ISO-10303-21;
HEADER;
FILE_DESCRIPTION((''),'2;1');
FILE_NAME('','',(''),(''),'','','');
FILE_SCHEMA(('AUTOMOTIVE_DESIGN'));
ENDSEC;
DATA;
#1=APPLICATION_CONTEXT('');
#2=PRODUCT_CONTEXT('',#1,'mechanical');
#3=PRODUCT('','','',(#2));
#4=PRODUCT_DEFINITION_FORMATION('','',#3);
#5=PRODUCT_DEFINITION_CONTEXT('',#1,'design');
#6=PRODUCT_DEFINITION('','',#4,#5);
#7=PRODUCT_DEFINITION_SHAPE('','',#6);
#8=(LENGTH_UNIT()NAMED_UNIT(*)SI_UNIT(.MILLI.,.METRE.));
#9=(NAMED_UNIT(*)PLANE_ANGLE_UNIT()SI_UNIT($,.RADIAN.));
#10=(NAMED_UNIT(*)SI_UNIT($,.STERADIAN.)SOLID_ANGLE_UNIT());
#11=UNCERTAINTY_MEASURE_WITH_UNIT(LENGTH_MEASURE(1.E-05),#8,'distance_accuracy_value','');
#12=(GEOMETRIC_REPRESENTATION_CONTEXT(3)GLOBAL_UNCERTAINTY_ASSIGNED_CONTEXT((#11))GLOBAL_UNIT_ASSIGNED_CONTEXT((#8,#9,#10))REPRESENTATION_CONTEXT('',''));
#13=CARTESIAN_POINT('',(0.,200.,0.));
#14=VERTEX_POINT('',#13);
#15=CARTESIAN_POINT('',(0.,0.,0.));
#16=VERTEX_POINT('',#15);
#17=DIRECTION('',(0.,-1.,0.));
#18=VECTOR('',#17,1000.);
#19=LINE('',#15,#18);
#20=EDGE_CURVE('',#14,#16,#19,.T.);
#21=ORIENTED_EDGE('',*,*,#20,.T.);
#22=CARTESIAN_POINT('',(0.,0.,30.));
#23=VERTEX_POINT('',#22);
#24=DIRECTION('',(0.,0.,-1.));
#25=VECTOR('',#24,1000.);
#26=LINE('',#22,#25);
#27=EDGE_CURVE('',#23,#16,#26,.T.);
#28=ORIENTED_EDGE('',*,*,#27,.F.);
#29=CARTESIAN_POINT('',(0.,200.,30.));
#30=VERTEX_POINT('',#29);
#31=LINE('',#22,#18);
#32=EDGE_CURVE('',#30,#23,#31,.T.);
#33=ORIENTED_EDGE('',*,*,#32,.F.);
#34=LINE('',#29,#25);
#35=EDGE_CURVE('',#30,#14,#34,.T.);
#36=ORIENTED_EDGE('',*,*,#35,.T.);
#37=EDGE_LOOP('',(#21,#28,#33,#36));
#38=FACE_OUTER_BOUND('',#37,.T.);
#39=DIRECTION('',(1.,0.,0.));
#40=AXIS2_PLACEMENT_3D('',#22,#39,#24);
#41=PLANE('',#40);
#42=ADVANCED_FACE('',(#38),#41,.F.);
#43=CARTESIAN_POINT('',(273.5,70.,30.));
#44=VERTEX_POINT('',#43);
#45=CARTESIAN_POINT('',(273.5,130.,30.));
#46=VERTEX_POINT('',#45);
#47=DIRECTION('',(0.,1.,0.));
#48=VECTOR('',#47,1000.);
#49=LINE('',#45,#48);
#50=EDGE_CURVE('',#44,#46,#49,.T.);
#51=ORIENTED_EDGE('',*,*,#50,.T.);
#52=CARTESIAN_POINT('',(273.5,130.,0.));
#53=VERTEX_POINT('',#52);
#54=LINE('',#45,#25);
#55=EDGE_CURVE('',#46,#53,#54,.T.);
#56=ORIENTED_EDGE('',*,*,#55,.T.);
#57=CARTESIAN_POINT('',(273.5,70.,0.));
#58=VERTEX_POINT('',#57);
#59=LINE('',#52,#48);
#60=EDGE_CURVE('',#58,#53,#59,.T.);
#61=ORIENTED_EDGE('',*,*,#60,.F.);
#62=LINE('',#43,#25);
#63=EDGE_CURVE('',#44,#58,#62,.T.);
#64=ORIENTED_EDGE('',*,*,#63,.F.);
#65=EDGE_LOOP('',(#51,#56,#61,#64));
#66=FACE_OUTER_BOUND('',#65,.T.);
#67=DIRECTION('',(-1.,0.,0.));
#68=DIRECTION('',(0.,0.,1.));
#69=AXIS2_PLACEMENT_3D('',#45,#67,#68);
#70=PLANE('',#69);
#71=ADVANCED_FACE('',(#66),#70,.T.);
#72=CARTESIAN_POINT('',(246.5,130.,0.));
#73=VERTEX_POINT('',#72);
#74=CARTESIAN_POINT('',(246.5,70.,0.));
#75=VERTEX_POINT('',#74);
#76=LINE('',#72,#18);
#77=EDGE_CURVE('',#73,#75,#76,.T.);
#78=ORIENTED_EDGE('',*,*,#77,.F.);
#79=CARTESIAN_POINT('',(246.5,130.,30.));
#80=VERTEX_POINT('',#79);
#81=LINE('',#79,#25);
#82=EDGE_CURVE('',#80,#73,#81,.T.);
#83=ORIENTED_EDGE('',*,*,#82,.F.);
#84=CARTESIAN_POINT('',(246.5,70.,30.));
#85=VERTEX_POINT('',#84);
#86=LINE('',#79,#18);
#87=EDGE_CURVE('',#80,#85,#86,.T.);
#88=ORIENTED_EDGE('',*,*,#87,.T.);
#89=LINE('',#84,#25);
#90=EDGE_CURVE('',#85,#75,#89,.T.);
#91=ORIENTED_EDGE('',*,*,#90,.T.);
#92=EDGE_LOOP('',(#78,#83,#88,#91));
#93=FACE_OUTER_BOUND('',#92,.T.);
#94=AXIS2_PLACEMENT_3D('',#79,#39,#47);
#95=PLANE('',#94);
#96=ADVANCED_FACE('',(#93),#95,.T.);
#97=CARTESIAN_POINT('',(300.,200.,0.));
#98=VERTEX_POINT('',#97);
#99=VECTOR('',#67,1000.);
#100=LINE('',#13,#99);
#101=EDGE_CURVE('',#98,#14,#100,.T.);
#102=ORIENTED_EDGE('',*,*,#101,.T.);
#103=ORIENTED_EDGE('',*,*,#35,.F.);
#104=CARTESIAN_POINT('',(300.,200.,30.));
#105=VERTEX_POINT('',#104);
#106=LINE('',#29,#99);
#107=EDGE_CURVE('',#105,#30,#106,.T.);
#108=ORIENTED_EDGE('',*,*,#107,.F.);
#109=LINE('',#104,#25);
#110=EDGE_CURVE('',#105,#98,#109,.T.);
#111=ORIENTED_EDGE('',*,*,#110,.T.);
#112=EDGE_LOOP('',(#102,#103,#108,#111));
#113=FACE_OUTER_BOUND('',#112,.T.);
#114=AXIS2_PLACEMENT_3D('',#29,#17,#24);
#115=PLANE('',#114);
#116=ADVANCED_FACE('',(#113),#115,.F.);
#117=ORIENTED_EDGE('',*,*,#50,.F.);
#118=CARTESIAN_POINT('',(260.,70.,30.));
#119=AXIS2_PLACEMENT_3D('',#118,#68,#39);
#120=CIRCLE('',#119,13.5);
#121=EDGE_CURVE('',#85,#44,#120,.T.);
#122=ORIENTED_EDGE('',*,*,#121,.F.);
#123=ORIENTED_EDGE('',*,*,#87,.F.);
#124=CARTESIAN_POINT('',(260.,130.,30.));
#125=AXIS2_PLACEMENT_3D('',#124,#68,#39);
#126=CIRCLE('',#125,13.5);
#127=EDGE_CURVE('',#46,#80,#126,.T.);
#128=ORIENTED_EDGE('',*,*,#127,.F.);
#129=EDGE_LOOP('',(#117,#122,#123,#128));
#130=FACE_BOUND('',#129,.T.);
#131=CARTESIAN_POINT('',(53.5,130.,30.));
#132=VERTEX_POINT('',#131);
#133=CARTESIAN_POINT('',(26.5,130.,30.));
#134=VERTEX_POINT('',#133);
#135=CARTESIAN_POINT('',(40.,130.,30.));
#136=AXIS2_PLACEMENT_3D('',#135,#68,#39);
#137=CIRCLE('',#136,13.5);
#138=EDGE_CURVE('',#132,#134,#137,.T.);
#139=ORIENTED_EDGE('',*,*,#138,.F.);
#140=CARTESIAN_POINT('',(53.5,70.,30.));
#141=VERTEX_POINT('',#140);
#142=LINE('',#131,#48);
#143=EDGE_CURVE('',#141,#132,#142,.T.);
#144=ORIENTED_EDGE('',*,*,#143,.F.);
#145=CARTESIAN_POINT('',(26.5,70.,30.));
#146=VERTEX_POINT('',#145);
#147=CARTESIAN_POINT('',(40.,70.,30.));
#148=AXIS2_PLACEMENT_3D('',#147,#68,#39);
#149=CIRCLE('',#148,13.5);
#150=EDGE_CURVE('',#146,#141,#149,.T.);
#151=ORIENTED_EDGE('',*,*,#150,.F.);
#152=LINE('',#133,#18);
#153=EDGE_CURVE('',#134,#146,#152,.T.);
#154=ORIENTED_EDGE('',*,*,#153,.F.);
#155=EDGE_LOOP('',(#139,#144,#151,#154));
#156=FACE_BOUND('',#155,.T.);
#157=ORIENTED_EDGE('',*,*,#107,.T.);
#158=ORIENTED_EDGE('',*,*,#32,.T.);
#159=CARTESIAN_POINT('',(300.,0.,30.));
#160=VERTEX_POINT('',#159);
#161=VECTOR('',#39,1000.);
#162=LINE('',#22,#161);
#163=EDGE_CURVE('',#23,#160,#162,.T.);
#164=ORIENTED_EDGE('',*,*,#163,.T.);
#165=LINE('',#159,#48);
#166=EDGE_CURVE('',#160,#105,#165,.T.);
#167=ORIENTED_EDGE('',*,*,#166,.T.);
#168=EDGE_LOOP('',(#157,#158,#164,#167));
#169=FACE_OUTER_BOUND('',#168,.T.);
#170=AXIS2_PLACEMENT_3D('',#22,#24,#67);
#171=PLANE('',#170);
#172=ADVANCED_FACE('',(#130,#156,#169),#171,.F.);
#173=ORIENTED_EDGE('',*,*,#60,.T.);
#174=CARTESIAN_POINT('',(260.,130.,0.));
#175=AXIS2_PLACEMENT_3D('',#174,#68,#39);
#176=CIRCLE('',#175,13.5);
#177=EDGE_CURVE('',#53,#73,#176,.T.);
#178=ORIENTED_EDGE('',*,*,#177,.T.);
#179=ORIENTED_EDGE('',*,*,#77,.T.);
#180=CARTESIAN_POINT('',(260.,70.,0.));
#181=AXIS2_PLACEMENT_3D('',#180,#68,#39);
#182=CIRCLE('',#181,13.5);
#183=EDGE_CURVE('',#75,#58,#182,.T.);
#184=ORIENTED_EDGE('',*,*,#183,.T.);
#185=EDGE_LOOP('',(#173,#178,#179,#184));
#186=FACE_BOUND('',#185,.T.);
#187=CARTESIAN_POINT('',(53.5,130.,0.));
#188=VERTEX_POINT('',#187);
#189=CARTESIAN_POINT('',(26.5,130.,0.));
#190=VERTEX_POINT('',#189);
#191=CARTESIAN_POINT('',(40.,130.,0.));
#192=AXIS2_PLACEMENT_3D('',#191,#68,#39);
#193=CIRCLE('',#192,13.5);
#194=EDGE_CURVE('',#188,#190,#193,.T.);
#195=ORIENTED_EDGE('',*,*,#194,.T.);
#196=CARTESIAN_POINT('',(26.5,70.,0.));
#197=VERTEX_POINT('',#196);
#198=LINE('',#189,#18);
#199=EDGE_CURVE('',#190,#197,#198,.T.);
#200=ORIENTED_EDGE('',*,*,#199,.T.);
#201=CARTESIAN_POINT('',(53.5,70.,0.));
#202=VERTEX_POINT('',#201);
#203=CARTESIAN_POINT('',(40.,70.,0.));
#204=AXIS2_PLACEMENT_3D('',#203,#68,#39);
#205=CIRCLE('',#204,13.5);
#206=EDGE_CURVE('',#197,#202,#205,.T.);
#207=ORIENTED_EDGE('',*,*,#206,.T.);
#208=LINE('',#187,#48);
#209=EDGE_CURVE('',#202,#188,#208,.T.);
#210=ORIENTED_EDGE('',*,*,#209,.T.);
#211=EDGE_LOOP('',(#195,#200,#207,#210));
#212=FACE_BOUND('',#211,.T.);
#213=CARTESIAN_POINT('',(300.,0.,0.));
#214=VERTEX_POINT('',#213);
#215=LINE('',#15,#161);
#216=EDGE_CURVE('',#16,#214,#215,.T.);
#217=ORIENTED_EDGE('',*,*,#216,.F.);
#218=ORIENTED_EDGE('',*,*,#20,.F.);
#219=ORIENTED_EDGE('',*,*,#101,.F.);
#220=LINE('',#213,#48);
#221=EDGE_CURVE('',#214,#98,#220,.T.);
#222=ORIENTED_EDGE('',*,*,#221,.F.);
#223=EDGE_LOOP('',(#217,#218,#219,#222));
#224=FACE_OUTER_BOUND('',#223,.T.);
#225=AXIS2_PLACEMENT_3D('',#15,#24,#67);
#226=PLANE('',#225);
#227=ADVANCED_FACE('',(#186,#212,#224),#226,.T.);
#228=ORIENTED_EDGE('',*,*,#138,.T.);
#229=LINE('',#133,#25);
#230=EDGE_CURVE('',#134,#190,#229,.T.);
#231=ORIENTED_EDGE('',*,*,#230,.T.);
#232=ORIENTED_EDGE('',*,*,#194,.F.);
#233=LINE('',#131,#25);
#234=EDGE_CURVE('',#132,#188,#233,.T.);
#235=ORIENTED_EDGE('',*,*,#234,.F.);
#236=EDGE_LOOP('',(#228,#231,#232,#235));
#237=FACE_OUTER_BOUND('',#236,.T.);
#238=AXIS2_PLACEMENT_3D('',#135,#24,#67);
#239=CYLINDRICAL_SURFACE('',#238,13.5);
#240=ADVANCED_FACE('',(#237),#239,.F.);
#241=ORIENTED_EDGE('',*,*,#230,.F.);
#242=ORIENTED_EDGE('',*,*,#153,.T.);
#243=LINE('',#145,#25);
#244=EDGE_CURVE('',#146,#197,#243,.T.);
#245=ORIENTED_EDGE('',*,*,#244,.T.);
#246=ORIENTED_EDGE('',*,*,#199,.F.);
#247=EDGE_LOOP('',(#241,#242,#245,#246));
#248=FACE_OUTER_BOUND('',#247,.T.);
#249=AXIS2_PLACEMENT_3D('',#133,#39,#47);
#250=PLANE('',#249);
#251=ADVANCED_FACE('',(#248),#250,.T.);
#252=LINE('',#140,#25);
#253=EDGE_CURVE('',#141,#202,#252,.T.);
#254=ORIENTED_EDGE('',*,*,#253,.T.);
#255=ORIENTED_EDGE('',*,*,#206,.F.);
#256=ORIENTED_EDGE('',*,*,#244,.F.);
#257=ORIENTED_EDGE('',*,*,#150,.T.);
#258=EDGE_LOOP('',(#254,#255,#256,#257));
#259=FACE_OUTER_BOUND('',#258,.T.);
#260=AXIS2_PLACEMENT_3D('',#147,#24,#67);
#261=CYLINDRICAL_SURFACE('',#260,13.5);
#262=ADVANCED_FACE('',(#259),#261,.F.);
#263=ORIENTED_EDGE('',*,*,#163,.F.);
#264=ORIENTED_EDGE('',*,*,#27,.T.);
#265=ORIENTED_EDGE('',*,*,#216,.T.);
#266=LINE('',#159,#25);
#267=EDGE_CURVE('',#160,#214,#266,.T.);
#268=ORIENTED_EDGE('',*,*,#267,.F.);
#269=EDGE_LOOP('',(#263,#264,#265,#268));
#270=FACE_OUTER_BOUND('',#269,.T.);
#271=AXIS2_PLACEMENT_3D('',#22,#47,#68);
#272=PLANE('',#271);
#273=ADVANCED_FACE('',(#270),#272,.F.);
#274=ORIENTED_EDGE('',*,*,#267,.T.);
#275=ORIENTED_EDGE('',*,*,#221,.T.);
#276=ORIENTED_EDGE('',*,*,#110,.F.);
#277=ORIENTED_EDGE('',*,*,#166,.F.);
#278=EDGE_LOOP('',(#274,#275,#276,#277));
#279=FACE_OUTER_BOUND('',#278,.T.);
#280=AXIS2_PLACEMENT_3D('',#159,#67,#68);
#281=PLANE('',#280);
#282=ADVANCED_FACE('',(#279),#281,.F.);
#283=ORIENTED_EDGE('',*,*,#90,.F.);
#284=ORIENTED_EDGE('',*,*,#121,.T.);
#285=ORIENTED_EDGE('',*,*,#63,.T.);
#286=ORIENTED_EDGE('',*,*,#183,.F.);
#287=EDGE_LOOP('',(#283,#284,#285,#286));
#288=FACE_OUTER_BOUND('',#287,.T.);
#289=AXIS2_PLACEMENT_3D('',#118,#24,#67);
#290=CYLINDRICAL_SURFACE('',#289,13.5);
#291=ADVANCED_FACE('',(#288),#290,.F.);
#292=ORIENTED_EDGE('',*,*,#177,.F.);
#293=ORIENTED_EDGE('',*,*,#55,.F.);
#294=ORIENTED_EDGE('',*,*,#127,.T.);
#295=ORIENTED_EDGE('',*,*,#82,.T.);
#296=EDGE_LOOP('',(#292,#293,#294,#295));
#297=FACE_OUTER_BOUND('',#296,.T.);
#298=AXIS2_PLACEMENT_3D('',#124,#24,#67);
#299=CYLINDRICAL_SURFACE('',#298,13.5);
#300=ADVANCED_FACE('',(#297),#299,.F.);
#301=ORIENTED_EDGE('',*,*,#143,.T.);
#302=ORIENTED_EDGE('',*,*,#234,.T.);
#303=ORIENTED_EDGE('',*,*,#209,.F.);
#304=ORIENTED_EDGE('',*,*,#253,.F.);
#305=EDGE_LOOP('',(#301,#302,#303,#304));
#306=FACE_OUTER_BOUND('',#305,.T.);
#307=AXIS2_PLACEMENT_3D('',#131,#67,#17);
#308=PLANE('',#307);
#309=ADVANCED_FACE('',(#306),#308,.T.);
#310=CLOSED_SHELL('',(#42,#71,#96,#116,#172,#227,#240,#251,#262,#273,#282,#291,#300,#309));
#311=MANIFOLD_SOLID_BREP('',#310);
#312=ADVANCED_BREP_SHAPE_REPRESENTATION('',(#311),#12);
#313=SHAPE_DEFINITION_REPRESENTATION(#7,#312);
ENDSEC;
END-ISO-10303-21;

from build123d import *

# Parameters (mm, degrees)
SKETCH1_W           = 300
SKETCH1_H           = 200
BOSS_EXTRUDE1_DEPTH = 30


with BuildPart() as part:
    # Sketch1 → Boss-Extrude1 (new body)
    with BuildSketch(Plane.XY):
        with Locations((150, 100)):
            Rectangle(SKETCH1_W, SKETCH1_H)
        with BuildLine():
            Line((273.5, 130), (273.5, 70))
            ThreePointArc((273.5, 70), (260, 56.5), (246.5, 70))
            Line((246.5, 70), (246.5, 130))
            ThreePointArc((246.5, 130), (260, 143.5), (273.5, 130))
        make_face(mode=Mode.SUBTRACT)
        with BuildLine():
            Line((53.5, 130), (53.5, 70))
            ThreePointArc((53.5, 70), (40, 56.5), (26.5, 70))
            Line((26.5, 70), (26.5, 130))
            ThreePointArc((26.5, 130), (40, 143.5), (53.5, 130))
        make_face(mode=Mode.SUBTRACT)
    extrude(amount=BOSS_EXTRUDE1_DEPTH)


solid = part.part
